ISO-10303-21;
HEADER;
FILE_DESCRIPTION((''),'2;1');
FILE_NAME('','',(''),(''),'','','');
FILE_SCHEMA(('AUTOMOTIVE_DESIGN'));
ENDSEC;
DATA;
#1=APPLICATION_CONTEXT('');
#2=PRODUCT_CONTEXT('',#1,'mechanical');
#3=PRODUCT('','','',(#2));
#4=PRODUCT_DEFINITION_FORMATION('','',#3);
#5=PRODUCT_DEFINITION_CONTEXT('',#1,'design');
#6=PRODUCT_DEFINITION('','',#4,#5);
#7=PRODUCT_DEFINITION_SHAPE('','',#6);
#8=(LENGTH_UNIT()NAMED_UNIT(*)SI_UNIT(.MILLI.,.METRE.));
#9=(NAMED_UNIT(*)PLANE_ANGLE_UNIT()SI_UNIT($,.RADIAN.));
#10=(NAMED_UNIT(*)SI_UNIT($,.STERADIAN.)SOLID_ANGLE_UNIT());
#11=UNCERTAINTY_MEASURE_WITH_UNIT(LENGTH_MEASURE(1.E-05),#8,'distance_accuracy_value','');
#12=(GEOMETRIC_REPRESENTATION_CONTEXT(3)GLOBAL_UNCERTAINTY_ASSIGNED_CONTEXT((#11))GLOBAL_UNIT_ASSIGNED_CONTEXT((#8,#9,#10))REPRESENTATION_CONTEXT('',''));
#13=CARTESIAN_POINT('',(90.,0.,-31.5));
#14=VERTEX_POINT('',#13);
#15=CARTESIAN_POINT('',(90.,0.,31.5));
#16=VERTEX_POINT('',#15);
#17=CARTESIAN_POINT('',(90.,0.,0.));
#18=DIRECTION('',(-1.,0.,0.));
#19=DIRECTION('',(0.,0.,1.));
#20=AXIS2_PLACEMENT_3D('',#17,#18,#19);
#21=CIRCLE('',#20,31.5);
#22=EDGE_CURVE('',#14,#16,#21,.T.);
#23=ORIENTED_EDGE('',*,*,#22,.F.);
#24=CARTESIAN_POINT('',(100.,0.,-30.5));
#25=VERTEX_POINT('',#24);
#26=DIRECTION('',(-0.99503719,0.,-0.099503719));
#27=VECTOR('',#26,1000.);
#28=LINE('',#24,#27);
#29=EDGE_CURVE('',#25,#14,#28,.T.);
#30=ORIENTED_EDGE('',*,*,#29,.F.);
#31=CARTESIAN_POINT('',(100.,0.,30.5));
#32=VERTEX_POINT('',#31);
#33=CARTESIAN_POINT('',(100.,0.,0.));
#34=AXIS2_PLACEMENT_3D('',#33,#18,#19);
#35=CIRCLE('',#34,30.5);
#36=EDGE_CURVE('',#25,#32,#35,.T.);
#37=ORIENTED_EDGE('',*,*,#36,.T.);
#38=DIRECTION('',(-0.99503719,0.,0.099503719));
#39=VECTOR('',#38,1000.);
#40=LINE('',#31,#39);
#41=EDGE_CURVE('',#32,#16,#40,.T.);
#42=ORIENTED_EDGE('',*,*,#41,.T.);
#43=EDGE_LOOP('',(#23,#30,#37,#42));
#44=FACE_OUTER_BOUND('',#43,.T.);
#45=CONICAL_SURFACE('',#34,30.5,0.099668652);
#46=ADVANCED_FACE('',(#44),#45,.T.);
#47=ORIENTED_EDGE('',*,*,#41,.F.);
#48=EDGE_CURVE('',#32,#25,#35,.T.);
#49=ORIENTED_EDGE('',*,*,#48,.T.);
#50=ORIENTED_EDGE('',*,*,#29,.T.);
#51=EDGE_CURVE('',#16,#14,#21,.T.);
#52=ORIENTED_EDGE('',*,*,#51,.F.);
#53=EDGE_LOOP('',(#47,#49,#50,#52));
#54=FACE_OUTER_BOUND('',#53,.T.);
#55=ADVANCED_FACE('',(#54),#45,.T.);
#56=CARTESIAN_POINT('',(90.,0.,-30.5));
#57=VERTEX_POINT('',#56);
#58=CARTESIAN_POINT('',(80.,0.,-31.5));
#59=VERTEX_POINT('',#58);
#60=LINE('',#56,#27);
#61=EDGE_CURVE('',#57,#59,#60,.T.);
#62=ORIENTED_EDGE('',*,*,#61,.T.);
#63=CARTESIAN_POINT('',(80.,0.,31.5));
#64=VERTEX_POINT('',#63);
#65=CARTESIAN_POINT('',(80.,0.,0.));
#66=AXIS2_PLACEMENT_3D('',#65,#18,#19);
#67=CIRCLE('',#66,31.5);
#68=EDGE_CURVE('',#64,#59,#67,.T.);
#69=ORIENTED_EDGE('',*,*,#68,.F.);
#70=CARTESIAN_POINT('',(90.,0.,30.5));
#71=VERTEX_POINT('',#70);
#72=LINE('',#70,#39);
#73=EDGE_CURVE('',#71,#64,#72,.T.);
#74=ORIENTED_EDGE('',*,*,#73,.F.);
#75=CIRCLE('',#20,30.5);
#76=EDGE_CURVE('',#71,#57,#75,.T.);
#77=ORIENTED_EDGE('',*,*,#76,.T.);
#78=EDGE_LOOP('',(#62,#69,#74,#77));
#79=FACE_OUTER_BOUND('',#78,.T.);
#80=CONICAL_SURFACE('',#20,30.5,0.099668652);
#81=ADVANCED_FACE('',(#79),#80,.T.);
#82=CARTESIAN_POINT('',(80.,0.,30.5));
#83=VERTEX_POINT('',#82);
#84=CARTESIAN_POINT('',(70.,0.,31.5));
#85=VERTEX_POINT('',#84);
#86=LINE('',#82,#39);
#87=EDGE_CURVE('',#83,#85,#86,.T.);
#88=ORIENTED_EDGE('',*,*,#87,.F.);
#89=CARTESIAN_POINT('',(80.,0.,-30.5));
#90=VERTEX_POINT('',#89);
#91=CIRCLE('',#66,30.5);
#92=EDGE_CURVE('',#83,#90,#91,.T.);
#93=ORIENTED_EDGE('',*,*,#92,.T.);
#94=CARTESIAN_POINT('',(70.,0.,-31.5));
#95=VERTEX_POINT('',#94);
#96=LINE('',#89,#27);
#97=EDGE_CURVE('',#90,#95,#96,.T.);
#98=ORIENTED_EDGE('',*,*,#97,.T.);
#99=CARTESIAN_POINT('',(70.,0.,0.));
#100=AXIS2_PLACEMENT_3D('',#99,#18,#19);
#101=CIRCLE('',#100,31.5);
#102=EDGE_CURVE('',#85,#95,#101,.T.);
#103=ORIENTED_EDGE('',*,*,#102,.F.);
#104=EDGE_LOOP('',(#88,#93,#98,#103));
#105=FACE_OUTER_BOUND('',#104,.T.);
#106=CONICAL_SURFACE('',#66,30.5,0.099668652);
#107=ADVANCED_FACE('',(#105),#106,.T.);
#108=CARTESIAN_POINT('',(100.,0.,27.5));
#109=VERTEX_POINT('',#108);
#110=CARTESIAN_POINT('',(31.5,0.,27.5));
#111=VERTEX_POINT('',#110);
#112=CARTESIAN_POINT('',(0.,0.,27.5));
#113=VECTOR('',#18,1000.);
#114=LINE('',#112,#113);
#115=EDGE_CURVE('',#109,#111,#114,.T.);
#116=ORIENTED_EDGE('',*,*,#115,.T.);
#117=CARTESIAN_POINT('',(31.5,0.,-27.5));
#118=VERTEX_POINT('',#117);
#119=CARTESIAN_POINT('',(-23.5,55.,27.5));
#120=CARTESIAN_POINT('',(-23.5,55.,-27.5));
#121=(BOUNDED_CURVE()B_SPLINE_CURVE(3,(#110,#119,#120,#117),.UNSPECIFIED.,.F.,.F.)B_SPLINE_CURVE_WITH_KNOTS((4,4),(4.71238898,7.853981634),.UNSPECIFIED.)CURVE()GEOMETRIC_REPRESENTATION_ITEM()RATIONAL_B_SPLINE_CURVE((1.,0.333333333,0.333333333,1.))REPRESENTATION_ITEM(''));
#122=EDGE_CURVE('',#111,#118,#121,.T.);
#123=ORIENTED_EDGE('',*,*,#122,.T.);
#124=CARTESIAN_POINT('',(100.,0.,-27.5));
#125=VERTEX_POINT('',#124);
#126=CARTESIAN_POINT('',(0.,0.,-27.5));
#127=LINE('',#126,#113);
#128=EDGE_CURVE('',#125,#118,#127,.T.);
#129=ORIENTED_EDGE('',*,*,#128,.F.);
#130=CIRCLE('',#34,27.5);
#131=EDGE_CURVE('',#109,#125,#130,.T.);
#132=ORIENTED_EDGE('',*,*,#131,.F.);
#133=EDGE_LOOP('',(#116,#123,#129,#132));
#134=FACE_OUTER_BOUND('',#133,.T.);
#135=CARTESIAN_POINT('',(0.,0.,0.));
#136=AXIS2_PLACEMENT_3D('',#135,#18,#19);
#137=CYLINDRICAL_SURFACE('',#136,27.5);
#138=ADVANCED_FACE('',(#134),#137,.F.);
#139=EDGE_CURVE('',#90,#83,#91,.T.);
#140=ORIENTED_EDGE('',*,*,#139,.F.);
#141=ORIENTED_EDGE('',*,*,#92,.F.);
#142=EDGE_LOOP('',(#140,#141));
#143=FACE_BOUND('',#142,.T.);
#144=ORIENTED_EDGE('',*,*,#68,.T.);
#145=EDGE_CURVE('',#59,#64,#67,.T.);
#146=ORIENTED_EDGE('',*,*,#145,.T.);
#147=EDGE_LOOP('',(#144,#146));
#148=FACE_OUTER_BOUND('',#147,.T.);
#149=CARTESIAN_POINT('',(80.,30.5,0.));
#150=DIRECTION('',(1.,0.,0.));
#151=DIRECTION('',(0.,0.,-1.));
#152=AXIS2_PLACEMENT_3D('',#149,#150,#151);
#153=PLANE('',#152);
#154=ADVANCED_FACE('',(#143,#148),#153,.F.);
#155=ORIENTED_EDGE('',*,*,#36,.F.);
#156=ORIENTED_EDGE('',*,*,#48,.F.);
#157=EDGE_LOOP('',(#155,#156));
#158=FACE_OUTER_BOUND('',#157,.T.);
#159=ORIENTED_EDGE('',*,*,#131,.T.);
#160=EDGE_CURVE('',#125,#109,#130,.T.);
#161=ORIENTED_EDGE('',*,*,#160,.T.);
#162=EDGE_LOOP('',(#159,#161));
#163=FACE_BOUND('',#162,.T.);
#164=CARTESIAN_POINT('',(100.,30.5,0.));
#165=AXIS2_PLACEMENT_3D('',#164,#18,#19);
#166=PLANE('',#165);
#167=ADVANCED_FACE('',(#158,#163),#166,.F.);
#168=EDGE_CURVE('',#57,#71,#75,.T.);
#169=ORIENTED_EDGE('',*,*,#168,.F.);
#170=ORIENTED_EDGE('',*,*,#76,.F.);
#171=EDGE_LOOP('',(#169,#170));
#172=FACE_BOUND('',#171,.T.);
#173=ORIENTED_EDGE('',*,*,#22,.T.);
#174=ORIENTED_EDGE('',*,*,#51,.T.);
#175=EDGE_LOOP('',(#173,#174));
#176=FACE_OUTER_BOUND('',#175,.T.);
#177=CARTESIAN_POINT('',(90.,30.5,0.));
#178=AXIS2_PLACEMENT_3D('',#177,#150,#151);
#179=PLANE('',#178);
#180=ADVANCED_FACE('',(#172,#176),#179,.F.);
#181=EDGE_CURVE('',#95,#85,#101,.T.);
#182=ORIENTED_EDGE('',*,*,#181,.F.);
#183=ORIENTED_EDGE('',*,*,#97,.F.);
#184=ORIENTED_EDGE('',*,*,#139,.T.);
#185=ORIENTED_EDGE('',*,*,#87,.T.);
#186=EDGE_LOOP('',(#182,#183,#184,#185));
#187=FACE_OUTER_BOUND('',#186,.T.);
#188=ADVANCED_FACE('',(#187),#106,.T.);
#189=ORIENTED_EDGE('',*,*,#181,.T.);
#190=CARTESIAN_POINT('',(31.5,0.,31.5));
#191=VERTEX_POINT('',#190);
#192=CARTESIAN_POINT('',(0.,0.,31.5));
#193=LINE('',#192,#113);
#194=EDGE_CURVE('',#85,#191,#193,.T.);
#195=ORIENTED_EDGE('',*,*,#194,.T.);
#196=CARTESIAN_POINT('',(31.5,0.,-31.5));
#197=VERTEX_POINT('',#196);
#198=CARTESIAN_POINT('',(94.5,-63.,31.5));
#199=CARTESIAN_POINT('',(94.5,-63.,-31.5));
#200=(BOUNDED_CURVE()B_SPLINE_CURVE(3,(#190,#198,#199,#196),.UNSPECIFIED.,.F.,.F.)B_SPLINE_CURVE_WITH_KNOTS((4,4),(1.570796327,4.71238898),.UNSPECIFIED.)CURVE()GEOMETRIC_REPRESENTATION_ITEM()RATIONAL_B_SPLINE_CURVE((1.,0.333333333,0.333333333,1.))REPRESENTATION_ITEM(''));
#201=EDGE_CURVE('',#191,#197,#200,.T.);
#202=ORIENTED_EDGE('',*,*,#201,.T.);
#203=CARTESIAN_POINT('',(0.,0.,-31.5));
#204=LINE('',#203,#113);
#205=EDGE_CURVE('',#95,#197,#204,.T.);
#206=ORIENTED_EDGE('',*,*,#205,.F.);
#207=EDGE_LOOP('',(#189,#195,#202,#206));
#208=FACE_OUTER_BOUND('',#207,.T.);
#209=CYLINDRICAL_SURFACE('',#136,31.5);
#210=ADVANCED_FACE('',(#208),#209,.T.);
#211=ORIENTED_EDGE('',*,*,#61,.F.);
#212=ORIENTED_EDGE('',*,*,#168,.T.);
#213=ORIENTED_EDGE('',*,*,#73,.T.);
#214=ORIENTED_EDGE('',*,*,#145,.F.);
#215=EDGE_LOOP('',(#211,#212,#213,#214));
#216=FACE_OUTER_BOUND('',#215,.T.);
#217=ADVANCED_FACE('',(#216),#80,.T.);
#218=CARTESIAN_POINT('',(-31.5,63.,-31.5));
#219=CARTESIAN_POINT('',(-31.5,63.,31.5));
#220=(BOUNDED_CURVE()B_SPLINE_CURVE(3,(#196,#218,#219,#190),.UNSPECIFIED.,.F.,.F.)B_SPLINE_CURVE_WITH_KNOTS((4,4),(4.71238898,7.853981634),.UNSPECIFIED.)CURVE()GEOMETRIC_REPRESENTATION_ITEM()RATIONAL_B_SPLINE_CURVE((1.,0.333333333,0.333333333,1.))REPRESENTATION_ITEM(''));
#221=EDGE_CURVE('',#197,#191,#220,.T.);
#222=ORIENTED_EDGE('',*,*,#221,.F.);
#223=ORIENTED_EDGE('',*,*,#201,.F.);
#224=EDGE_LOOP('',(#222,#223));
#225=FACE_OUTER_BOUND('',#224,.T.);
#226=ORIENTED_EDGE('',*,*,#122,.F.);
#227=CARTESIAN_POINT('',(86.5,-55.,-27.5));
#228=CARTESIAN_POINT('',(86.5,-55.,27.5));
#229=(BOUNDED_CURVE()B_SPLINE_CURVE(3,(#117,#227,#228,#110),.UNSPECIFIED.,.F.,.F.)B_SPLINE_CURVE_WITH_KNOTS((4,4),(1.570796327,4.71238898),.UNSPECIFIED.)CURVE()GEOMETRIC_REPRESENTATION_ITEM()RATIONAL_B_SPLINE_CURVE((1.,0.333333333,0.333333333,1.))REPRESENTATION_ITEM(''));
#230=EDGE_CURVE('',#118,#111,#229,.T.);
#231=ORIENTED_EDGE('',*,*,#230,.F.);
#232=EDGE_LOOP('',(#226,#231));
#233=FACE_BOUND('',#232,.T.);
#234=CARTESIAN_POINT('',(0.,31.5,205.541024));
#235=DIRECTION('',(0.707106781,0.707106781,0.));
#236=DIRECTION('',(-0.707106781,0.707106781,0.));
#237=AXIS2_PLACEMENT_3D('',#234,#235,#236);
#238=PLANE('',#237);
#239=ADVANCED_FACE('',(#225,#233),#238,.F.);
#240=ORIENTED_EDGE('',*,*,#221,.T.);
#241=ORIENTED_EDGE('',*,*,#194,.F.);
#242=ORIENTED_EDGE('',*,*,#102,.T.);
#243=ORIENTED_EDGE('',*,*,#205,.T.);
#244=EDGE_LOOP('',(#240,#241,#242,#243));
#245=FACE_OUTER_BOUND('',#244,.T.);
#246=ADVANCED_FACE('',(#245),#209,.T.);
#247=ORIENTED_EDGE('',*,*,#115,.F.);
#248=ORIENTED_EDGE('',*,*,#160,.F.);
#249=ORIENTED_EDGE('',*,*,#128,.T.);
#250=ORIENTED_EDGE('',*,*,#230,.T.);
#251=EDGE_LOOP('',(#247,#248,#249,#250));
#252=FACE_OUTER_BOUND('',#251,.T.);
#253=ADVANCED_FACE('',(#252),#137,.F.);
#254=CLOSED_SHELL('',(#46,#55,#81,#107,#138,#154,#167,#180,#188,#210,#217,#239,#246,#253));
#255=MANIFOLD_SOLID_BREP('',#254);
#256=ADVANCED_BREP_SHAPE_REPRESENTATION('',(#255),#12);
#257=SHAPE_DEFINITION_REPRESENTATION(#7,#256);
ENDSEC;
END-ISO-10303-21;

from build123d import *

# Parameters (mm, degrees)
CUT_EXTRUDE1_DEPTH      = 110.473741144
CUT_EXTRUDE1_DEPTH_BACK = 110.473741144


with BuildPart() as part:
    # Sketch1 → Revolve1 (revolve)
    with BuildSketch(Plane.XY, mode=Mode.PRIVATE) as revolve1_sk:
        Polygon((0, 27.5), (0, 31.5), (70, 31.5), (80, 30.5), (80, 31.5), (90, 30.5), (90, 31.5), (100, 30.5), (100, 27.5), align=None)
    revolve(revolve1_sk.sketch.rotate(Axis((0, 0, 0), (1, 0, 0)), 90), axis=Axis((0, 0, 0), (1, 0, 0)))

    # Sketch2 → Cut-Extrude1 (cut, two sides: drawn at the far end of the back side and taken through both)
    with BuildSketch(Plane.XY.offset(-CUT_EXTRUDE1_DEPTH_BACK)):
        Polygon((-199.7384521, 231.2384521), (0, 31.5), (96.333692144, -64.833692144), (296.072144244, -264.572144244), (-103.404759956, -664.049048445), (-599.2153563, -168.2384521), align=None)
    extrude(amount=CUT_EXTRUDE1_DEPTH + CUT_EXTRUDE1_DEPTH_BACK, mode=Mode.SUBTRACT)


solid = part.part
